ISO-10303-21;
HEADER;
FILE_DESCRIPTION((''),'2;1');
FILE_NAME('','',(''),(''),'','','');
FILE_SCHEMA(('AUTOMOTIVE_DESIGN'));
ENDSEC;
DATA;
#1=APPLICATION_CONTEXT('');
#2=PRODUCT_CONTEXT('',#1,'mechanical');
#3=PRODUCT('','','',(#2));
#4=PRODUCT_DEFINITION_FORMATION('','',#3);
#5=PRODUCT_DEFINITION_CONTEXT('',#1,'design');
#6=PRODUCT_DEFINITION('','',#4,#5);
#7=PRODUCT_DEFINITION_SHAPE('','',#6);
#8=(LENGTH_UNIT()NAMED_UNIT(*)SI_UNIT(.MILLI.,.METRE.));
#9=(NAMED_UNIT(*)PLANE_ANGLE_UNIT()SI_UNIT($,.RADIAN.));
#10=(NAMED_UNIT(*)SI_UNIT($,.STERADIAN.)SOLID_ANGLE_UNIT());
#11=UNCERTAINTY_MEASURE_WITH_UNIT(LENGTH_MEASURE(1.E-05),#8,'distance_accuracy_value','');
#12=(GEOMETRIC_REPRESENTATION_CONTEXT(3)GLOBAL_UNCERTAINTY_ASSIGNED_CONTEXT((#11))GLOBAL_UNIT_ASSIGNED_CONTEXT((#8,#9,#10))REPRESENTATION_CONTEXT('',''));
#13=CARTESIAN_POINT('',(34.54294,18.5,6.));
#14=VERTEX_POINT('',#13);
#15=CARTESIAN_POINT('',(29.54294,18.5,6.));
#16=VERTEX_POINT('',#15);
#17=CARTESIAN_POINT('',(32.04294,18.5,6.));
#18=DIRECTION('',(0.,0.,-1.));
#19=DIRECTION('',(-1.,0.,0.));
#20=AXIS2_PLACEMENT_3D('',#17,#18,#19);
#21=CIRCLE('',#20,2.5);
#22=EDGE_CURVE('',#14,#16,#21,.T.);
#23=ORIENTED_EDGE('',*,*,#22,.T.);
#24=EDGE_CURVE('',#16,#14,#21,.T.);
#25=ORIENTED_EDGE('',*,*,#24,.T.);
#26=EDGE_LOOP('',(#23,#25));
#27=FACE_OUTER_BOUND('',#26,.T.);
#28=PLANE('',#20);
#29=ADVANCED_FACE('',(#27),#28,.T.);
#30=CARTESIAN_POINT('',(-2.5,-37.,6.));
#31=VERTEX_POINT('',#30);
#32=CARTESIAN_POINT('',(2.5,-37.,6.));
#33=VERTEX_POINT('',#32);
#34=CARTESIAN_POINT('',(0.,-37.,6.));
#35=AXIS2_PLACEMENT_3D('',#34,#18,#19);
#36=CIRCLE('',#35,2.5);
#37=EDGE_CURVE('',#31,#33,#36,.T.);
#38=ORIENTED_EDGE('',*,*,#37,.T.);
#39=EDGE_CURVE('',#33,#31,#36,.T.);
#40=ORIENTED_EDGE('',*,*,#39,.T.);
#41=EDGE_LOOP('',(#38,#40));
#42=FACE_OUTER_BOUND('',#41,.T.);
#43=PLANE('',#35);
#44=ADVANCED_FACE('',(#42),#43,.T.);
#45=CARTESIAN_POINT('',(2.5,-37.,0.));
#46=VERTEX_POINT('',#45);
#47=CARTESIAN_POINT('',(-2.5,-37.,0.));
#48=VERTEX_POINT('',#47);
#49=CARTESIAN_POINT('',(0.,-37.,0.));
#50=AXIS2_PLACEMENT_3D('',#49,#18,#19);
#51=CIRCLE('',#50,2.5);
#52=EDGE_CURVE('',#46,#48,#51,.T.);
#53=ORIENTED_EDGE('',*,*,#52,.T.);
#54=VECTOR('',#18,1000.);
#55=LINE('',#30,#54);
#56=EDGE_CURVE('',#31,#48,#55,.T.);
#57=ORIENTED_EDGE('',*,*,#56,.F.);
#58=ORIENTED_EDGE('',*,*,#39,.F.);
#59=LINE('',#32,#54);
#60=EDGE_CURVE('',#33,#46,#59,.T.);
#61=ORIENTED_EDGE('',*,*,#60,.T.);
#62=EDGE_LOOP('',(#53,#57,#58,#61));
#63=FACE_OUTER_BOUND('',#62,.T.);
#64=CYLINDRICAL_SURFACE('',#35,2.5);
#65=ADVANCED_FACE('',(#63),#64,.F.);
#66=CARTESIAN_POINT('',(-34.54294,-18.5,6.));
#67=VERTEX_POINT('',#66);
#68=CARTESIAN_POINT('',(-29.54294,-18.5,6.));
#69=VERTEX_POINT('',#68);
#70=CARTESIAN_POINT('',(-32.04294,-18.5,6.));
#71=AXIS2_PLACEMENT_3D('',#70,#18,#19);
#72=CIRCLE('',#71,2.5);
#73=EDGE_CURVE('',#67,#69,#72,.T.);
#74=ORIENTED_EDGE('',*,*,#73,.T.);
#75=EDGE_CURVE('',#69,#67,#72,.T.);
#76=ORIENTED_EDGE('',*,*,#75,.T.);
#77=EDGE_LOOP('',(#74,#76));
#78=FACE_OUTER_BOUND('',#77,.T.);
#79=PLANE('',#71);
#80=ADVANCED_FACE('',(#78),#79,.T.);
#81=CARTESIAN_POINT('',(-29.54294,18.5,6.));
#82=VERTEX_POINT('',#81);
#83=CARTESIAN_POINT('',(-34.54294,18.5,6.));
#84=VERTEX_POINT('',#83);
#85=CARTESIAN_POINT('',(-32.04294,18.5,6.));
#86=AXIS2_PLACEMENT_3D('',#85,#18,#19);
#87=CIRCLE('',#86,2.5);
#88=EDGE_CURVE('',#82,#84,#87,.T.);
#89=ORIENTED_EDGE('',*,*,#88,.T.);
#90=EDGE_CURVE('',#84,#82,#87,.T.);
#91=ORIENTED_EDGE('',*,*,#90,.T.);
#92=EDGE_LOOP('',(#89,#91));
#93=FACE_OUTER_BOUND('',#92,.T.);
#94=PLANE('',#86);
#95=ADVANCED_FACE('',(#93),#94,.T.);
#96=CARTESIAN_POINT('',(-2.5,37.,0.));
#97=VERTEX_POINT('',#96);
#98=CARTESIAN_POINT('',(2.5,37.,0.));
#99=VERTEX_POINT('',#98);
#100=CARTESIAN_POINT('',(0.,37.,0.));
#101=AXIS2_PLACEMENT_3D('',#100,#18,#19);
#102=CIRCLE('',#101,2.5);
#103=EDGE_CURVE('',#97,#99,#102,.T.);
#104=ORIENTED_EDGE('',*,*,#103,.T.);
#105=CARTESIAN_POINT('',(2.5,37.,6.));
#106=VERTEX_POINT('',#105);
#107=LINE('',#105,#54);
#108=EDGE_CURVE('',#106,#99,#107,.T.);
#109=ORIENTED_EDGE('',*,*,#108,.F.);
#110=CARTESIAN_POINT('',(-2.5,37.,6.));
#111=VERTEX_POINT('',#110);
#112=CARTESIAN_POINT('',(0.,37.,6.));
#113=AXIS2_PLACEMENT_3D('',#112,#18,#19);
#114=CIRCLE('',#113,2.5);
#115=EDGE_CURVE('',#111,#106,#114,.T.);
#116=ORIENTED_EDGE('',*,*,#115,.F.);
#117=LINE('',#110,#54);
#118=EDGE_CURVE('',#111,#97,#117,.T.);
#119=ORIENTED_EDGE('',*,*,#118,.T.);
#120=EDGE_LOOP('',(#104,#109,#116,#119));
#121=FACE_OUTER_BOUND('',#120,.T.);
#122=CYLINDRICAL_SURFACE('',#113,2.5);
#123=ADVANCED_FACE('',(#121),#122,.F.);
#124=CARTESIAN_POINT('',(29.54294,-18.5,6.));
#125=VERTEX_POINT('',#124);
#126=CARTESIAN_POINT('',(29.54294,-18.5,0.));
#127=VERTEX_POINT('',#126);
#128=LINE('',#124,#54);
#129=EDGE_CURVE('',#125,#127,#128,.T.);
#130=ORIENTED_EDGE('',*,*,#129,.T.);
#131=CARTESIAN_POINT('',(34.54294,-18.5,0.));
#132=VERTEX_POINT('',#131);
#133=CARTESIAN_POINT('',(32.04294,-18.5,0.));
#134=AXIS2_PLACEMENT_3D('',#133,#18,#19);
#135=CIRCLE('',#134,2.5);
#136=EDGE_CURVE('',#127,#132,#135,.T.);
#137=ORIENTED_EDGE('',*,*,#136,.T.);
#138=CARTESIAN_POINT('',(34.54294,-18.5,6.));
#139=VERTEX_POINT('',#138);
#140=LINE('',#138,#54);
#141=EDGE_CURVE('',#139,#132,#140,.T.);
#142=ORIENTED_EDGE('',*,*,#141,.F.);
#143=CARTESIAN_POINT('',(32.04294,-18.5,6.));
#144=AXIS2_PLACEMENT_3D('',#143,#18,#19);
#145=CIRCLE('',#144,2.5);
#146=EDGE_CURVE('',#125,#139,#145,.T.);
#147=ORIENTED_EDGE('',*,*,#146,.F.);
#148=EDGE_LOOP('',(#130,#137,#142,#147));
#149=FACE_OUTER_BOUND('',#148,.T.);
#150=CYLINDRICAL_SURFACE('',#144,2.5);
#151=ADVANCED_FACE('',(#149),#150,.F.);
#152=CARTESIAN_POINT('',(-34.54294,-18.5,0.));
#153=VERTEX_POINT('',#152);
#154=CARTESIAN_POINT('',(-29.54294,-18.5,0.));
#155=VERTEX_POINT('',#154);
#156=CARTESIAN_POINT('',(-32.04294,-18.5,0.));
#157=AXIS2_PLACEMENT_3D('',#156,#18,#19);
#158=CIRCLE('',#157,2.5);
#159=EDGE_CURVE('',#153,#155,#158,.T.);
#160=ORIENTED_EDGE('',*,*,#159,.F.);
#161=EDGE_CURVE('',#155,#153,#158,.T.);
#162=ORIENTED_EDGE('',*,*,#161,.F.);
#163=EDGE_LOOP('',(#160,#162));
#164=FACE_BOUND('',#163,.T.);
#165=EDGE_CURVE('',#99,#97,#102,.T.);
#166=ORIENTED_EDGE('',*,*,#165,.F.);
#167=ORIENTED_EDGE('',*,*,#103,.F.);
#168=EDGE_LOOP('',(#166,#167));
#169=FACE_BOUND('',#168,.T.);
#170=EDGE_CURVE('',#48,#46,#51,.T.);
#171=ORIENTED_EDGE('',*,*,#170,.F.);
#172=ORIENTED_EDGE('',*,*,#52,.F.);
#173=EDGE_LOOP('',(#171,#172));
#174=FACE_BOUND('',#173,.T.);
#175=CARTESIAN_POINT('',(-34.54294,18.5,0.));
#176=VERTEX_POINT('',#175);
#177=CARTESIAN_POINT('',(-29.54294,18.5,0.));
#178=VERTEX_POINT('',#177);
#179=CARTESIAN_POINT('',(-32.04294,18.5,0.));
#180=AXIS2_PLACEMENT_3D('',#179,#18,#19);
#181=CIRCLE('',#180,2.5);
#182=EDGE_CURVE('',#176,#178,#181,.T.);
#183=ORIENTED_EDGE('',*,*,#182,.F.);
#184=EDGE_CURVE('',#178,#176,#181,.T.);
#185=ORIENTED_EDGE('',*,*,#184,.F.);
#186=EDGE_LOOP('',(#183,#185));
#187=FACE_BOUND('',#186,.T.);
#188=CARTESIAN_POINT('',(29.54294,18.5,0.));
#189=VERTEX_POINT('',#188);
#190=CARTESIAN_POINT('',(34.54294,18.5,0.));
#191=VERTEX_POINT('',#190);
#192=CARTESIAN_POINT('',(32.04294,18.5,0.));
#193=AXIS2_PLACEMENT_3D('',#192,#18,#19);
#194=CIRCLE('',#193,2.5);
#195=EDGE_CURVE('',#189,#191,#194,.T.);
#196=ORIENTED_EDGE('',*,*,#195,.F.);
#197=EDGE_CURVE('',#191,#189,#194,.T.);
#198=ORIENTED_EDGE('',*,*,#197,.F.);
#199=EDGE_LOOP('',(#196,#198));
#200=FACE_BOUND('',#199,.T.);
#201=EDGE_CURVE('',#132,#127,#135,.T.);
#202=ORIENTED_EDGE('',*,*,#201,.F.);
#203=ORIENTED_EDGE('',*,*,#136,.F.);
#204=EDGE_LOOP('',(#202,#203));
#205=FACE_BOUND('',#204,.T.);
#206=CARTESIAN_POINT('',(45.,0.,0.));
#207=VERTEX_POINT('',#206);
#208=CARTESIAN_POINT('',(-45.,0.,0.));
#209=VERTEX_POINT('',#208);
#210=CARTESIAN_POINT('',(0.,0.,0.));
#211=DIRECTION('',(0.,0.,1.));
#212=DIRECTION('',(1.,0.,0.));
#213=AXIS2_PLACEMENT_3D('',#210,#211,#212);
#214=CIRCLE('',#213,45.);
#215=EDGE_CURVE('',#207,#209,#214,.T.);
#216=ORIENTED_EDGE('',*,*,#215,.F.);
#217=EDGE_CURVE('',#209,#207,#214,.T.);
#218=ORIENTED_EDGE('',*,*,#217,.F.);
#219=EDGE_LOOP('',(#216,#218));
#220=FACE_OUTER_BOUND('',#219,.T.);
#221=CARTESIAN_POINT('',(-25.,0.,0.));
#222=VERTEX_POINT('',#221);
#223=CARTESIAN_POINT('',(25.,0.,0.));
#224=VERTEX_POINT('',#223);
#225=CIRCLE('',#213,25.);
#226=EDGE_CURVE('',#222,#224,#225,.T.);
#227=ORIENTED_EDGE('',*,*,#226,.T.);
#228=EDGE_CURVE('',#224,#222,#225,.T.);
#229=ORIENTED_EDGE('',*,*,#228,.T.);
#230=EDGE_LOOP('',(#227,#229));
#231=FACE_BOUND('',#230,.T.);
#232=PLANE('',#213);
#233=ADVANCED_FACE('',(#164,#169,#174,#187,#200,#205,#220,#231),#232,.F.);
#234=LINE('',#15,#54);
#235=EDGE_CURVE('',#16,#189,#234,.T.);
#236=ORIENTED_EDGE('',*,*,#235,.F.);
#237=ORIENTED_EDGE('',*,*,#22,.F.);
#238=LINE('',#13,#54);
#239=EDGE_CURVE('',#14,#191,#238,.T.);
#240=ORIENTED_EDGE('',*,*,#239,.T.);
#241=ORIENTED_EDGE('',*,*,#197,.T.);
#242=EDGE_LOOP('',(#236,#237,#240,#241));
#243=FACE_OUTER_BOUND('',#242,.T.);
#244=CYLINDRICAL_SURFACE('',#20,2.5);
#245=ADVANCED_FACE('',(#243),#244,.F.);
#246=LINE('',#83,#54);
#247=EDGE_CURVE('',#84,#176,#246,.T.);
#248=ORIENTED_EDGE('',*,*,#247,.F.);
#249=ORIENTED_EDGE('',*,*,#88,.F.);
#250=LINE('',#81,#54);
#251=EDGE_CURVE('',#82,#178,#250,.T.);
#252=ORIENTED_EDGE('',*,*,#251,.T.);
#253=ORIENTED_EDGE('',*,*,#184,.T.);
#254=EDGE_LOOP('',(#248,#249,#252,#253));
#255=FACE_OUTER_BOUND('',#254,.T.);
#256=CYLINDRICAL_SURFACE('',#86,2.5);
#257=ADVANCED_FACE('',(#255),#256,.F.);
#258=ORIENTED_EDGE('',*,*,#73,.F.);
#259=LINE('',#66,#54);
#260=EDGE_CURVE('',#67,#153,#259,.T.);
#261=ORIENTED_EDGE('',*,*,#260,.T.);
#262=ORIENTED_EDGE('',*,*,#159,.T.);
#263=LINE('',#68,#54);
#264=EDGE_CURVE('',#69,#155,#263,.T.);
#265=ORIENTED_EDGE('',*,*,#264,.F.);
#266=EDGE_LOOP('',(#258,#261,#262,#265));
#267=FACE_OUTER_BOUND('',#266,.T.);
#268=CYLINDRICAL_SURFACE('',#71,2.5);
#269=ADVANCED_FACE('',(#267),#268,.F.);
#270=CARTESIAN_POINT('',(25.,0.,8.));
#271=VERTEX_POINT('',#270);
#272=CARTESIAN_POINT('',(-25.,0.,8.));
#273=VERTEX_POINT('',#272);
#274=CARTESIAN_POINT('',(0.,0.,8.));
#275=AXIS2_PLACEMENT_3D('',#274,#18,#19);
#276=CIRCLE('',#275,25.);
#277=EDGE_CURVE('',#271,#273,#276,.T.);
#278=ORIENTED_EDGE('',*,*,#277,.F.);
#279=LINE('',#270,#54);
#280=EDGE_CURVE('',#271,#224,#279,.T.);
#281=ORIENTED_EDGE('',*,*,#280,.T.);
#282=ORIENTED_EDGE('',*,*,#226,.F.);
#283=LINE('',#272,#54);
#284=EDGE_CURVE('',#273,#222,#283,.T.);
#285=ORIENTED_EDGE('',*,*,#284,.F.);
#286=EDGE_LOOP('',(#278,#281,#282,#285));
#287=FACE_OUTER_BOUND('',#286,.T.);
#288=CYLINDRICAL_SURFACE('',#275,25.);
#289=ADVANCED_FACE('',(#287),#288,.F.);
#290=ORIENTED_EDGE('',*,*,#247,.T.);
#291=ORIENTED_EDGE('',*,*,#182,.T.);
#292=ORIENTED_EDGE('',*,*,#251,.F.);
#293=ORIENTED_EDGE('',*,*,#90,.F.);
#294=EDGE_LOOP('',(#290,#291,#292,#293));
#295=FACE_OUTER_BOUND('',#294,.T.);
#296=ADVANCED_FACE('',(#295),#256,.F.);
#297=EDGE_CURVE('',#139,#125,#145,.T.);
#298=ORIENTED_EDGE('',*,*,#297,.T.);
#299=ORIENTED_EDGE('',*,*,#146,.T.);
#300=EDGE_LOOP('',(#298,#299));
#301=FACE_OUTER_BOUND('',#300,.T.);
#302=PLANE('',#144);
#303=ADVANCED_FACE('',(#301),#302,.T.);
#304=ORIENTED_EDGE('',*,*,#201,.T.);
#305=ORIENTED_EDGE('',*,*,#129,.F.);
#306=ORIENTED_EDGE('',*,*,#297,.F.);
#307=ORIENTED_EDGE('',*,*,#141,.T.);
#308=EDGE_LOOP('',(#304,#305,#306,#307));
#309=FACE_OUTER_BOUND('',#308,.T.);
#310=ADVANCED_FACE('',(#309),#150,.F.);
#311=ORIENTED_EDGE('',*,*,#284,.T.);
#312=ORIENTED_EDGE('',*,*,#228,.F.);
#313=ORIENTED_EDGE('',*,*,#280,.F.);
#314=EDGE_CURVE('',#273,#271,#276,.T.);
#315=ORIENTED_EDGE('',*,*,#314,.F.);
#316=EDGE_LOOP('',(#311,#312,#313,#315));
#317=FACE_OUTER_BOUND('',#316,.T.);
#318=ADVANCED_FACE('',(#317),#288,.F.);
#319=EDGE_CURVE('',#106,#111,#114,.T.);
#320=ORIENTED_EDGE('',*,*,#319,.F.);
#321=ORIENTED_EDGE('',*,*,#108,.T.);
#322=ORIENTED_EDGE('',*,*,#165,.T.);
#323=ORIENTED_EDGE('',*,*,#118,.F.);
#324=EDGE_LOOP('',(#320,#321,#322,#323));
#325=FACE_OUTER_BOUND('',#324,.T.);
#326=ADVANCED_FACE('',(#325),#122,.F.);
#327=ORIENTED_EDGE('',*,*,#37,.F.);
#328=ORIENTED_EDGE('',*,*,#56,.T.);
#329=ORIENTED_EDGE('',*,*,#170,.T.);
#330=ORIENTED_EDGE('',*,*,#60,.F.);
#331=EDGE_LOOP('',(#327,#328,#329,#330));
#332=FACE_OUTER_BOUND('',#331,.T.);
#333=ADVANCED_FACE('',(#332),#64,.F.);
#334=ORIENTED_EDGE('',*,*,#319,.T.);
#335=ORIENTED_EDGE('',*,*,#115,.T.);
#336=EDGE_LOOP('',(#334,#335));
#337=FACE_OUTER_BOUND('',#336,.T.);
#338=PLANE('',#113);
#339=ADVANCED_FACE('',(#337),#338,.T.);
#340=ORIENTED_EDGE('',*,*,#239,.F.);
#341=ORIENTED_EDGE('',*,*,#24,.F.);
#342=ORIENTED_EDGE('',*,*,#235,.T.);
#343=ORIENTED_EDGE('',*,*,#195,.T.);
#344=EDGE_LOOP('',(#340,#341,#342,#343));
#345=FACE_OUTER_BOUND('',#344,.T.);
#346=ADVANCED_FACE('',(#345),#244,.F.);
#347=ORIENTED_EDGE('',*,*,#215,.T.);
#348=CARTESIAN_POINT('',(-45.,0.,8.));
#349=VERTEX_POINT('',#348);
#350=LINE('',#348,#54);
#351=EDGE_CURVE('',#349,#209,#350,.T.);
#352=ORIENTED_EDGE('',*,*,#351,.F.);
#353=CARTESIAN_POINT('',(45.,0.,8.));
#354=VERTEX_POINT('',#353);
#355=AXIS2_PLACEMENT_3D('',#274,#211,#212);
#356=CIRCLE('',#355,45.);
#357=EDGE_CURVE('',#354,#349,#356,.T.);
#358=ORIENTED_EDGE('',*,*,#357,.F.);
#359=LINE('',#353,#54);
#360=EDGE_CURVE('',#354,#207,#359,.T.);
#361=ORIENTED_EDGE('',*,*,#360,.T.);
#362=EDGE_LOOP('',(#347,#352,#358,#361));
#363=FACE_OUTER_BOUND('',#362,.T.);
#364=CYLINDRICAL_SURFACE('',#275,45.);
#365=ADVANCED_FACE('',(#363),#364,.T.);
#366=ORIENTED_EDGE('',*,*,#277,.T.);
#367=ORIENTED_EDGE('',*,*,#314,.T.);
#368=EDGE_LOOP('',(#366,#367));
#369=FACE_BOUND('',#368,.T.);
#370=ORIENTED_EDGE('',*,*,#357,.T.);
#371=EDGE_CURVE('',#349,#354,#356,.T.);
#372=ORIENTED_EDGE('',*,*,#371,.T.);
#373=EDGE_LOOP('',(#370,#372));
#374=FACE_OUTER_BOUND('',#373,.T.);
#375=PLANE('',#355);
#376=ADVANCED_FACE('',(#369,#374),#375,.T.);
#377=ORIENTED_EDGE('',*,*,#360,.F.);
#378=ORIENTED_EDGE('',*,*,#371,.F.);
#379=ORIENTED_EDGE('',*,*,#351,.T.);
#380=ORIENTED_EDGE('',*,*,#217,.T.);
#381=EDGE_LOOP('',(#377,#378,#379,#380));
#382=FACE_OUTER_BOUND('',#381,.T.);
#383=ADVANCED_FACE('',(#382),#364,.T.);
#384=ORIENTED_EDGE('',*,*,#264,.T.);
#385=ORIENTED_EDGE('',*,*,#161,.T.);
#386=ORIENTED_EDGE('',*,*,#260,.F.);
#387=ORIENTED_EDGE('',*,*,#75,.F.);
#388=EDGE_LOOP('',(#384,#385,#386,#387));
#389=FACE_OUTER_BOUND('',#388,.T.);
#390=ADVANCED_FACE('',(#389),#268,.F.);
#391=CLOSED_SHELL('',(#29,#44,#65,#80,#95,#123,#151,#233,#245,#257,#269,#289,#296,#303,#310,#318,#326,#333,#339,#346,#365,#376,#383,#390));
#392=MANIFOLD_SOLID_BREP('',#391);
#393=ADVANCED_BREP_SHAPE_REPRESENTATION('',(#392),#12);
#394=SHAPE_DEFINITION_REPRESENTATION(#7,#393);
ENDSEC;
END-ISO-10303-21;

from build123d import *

# Parameters (mm, degrees)
SKETCH1_R           = 45
SKETCH1_R_2         = 25
BOSS_EXTRUDE1_DEPTH = 8
SKETCH2_R           = 42
SKETCH2_R_2         = 25
BOSS_EXTRUDE2_DEPTH = 3
SKETCH3_R           = 2.5
CUT_EXTRUDE1_DEPTH  = 6
CHAMFER1_SIZE       = 1
SKETCH4_R           = 42
SKETCH4_R_2         = 55
CUT_EXTRUDE2_DEPTH  = 3


with BuildPart() as part:
    # Sketch1 → Boss-Extrude1 (new body)
    with BuildSketch(Plane.XY):
        Circle(SKETCH1_R)
        Circle(SKETCH1_R_2, mode=Mode.SUBTRACT)
    extrude(amount=BOSS_EXTRUDE1_DEPTH)

    # Sketch2 → Boss-Extrude2 (add)
    with BuildSketch(Plane.XY.offset(8)):
        Circle(SKETCH2_R)
        Circle(SKETCH2_R_2, mode=Mode.SUBTRACT)
    extrude(amount=BOSS_EXTRUDE2_DEPTH)

    # Sketch3 → Cut-Extrude1 (cut)
    with BuildSketch(Plane(origin=(0, 0, 0), x_dir=(-1, 0, 0), z_dir=(0, 0, -1))):
        with Locations((0, 37)):
            Circle(SKETCH3_R)
        with Locations((32.04293994, 18.5)):
            Circle(SKETCH3_R)
        with Locations((32.04293994, -18.5)):
            Circle(SKETCH3_R)
        with Locations((0, -37)):
            Circle(SKETCH3_R)
        with Locations((-32.04293994, -18.5)):
            Circle(SKETCH3_R)
        with Locations((-32.04293994, 18.5)):
            Circle(SKETCH3_R)
    extrude(amount=-CUT_EXTRUDE1_DEPTH, mode=Mode.SUBTRACT)

    # Chamfer1
    chamfer1_edges = [part.edges().sort_by_distance(p)[0] for p in [
        (-42, 0, 11),
        (-25, 0, 11),
    ]]
    chamfer(chamfer1_edges, length=CHAMFER1_SIZE)

    # Sketch4 → Cut-Extrude2 (cut)
    with BuildSketch(Plane(origin=(248.99389391, -65.332745645, 8), x_dir=(0.8404902422792763, -0.5418266813597531, 0), z_dir=(0, 0, -1))):
        with Locations((-244.675962976, 80)):
            Circle(SKETCH4_R)
        with Locations((-244.675962976, -130)):
            Circle(SKETCH4_R_2)
    extrude(amount=-CUT_EXTRUDE2_DEPTH, mode=Mode.SUBTRACT)


solid = part.part
